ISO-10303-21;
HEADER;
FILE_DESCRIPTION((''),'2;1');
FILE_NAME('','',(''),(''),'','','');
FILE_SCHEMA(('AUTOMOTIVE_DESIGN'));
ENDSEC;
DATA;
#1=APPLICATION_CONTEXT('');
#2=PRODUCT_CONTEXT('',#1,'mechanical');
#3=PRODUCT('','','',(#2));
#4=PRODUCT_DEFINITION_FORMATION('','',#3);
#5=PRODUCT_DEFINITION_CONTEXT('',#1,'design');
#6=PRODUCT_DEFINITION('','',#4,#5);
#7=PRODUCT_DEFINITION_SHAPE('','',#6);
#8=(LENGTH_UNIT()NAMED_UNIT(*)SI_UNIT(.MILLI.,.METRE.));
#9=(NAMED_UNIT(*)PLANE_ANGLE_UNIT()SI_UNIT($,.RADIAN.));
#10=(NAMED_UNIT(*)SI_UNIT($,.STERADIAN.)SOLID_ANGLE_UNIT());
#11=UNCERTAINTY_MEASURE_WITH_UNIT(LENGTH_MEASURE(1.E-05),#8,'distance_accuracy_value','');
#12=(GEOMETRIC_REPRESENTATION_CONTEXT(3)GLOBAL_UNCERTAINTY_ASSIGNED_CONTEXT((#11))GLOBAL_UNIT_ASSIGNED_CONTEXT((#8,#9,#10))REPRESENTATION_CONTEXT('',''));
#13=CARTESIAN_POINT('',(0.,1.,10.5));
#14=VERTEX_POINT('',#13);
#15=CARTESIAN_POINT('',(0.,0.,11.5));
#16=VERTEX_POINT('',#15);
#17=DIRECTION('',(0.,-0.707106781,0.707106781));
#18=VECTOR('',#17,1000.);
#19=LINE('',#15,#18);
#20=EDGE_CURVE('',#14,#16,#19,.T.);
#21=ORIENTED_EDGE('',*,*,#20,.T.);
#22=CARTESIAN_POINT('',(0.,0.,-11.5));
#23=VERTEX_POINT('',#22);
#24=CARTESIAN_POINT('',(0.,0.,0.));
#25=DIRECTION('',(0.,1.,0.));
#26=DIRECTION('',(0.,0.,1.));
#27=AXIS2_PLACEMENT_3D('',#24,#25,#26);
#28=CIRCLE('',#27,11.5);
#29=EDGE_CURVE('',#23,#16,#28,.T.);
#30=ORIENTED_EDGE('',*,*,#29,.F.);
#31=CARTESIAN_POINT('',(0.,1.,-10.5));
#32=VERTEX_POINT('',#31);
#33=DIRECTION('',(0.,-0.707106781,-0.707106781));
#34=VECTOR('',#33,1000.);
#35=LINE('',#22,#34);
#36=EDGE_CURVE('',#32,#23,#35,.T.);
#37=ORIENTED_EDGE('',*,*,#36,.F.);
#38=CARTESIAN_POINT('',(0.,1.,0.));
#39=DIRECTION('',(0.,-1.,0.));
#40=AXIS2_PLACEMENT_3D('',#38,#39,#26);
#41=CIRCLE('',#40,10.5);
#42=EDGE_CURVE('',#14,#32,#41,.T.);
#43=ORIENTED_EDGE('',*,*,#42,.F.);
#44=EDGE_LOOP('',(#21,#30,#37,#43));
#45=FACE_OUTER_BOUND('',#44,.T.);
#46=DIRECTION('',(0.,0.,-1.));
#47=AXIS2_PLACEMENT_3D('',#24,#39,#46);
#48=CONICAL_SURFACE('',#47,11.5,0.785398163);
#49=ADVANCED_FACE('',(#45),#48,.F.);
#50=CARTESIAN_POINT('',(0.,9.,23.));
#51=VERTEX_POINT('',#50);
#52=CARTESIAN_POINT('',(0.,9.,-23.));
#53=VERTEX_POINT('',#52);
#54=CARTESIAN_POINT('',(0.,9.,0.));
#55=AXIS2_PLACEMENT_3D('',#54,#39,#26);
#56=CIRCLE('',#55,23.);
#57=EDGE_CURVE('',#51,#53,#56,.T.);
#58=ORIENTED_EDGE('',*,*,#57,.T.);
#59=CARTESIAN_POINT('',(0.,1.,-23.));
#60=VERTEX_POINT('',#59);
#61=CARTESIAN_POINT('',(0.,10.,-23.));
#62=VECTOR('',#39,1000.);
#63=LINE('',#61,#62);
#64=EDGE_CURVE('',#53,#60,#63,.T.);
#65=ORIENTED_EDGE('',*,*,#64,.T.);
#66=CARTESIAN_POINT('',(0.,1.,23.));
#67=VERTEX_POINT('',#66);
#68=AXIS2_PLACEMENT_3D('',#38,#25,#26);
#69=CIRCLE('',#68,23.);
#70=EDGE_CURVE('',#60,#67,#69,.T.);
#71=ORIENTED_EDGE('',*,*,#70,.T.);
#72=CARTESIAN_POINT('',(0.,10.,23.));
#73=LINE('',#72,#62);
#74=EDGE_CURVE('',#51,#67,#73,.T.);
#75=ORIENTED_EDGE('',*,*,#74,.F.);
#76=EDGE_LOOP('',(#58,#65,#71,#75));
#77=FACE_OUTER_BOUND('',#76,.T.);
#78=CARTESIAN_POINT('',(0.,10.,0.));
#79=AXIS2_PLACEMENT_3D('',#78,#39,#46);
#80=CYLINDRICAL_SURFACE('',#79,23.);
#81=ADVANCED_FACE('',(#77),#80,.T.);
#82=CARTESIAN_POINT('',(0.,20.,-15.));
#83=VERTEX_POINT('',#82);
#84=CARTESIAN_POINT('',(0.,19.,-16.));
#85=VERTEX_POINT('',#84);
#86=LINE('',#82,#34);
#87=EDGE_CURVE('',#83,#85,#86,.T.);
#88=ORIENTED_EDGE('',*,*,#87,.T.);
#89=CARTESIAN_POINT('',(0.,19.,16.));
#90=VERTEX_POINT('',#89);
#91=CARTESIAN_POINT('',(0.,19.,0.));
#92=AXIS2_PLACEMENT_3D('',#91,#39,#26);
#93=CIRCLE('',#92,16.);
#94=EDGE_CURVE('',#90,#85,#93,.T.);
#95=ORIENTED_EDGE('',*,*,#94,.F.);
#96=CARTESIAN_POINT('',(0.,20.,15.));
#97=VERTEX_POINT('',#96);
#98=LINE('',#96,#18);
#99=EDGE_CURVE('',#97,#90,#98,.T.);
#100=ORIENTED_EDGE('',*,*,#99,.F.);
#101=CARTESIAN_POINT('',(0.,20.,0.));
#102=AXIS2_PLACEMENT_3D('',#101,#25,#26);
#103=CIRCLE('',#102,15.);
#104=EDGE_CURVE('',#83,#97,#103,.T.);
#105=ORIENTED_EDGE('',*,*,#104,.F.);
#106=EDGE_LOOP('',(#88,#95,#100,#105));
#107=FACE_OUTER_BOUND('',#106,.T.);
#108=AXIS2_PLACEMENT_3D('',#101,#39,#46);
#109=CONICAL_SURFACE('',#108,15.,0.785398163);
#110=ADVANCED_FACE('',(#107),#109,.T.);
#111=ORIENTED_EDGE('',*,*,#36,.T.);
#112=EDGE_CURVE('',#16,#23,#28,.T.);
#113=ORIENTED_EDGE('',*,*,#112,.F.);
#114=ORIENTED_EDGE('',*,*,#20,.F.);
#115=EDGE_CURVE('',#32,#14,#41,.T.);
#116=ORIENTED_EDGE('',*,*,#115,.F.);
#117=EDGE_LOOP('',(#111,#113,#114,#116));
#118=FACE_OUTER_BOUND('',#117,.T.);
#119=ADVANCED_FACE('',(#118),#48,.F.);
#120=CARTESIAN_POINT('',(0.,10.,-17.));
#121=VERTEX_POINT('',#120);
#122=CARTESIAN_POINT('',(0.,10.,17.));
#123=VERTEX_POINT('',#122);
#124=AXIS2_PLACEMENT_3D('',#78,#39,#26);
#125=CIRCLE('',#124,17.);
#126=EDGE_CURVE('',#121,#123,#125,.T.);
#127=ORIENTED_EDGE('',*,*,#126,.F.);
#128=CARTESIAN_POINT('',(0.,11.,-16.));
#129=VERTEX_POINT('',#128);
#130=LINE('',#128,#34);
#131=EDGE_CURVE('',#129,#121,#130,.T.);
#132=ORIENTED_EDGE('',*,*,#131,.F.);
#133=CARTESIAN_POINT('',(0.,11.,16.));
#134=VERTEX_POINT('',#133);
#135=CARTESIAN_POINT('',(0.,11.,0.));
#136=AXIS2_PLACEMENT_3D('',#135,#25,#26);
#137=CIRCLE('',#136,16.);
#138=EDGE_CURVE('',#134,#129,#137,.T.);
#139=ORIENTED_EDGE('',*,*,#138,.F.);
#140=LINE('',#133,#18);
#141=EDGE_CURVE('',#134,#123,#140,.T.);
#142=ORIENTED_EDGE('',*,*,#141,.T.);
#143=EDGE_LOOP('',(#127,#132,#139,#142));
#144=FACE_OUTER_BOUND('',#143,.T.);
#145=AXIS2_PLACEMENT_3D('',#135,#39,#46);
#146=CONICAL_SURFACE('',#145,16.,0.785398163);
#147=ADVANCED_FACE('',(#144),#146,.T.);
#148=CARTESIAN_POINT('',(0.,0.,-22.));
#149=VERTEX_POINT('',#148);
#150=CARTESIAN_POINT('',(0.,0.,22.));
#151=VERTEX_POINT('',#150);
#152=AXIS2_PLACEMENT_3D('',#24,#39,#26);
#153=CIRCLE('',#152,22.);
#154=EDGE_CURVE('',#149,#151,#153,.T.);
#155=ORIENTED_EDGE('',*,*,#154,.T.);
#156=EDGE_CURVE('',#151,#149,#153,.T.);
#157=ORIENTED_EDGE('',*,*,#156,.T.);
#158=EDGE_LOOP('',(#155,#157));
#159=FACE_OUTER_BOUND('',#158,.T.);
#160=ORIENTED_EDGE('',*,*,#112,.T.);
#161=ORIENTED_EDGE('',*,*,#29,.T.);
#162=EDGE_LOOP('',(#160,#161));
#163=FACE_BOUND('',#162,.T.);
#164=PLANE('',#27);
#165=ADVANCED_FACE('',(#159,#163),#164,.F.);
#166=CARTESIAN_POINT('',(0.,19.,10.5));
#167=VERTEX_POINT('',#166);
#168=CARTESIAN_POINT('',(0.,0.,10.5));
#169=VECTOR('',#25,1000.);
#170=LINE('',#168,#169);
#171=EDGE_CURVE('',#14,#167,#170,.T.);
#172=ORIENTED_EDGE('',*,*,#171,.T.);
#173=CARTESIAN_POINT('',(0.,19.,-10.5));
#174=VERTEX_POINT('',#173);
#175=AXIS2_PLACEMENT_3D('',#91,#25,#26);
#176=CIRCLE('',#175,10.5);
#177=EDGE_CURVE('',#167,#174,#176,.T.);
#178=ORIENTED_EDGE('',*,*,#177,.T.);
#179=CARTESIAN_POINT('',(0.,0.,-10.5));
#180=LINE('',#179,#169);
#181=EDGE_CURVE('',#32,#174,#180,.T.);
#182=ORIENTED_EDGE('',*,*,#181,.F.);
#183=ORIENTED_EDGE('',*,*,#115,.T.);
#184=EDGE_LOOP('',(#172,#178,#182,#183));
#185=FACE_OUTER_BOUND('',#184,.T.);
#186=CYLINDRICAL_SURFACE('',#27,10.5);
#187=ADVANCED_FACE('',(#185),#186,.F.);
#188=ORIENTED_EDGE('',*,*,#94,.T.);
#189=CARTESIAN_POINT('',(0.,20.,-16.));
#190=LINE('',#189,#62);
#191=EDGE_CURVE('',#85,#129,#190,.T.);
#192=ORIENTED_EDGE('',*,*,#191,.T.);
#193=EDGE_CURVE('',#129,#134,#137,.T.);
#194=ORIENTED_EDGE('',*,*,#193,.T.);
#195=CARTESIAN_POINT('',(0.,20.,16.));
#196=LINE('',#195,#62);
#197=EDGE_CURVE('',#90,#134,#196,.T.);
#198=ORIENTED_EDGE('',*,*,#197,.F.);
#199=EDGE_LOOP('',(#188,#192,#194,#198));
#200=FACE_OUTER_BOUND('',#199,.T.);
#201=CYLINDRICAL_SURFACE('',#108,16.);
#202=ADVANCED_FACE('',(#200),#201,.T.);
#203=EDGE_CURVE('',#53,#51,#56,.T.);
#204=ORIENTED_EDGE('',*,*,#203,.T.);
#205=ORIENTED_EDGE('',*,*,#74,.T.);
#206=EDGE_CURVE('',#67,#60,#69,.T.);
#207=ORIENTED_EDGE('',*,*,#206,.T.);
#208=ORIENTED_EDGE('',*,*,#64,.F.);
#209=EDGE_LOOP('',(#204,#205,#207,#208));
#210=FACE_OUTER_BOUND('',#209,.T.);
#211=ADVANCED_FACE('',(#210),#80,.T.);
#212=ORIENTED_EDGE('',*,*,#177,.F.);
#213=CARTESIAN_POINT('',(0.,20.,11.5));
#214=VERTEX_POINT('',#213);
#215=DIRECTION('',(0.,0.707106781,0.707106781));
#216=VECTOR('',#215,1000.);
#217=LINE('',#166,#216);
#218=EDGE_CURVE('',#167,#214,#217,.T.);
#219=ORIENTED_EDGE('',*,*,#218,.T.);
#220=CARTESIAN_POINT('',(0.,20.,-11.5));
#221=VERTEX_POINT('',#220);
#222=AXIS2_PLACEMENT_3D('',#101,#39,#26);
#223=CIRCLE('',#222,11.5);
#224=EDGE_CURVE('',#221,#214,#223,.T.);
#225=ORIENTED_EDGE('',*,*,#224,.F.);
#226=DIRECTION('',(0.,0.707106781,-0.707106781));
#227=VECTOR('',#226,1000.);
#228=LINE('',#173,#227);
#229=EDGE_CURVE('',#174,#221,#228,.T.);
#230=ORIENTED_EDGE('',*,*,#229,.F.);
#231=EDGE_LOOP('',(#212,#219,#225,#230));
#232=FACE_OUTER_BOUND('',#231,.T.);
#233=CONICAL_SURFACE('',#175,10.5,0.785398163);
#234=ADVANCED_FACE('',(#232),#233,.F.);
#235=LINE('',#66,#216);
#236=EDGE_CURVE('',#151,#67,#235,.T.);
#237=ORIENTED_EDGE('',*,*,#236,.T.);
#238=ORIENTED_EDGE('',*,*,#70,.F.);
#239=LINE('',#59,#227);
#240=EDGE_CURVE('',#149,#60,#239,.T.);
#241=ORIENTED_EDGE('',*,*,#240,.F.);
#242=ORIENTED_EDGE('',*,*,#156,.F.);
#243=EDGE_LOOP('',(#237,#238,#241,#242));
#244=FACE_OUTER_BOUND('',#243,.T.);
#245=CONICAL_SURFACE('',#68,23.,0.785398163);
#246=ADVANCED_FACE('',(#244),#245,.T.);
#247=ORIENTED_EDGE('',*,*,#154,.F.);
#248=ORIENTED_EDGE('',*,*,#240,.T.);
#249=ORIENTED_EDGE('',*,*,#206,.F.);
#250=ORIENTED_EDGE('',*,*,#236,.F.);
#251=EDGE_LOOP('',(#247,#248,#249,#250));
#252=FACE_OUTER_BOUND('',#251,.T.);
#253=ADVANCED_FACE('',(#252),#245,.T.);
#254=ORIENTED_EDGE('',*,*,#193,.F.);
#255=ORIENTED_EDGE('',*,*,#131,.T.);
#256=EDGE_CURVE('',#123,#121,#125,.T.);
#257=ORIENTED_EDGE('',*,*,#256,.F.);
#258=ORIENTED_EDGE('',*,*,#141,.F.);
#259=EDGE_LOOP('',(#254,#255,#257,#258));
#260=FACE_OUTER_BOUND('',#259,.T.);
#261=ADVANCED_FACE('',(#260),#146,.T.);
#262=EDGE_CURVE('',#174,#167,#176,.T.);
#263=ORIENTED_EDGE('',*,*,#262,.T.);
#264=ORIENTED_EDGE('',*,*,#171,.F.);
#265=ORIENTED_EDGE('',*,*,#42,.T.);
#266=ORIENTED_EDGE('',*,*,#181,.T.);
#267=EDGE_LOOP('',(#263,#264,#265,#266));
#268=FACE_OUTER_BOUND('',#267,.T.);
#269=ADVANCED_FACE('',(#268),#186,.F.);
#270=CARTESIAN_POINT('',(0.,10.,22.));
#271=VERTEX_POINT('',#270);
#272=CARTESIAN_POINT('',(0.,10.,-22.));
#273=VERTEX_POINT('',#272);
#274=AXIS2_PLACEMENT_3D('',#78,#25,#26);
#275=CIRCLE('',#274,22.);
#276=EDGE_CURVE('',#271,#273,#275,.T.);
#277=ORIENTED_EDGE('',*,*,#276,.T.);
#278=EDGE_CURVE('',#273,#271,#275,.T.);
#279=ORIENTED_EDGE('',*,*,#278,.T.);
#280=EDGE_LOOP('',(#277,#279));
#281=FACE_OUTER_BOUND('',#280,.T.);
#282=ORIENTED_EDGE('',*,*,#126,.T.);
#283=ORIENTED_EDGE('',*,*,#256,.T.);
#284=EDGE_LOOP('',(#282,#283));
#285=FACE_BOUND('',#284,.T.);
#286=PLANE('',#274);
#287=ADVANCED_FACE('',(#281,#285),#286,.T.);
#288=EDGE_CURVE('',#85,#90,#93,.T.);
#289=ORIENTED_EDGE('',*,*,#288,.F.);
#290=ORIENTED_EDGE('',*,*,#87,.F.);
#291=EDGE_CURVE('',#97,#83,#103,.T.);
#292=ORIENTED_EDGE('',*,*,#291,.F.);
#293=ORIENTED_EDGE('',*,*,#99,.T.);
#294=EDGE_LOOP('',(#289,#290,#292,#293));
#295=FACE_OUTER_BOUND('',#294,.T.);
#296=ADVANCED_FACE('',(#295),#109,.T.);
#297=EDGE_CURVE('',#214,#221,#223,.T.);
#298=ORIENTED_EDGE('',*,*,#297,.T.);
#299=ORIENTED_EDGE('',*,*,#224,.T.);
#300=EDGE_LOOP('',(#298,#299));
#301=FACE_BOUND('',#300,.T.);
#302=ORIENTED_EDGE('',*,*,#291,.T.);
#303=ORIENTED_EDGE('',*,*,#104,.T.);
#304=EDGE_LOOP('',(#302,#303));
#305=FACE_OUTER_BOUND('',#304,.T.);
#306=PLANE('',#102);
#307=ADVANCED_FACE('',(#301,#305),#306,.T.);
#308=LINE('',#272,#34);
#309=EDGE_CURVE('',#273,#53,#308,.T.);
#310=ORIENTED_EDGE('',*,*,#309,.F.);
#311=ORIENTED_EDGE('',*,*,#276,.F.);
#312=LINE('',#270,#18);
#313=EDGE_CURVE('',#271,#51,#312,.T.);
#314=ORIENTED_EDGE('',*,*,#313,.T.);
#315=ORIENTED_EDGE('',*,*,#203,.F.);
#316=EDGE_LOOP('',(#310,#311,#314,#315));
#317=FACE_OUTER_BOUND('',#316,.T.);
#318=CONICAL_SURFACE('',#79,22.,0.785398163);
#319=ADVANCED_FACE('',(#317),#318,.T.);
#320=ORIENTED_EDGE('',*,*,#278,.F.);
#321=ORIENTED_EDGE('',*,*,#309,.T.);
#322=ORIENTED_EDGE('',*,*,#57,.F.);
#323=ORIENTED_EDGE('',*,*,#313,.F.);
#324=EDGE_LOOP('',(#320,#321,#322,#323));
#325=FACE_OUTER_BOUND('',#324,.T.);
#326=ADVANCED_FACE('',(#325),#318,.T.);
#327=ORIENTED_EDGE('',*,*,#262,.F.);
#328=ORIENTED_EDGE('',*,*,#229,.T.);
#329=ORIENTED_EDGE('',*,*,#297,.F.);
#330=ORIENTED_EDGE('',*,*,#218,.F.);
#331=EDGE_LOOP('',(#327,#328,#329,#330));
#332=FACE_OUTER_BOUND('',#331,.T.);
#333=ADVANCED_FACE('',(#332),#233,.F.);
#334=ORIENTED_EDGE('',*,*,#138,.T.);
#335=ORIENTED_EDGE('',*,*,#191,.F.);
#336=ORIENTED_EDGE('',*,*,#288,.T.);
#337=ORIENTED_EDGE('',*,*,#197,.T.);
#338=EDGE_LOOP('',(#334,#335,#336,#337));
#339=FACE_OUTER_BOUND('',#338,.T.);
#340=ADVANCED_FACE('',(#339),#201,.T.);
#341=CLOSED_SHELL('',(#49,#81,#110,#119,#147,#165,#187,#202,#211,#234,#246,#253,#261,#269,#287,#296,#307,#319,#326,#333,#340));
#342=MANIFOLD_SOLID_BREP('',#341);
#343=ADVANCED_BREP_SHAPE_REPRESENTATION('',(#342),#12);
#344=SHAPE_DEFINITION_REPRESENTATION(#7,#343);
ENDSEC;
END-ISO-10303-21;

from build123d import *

# Parameters (mm, degrees)
SKETCH1_R           = 23
BOSS_EXTRUDE1_DEPTH = 10
SKETCH2_R           = 16
BOSS_EXTRUDE2_DEPTH = 10
SKETCH3_R           = 10.5
CUT_EXTRUDE1_DEPTH  = 20
CHAMFER1_SIZE       = 1
CHAMFER2_SIZE       = 1


with BuildPart() as part:
    # Sketch1 → Boss-Extrude1 (new body)
    with BuildSketch(Plane(origin=(0, 0, 0), x_dir=(1, 0, 0), z_dir=(0, 1, 0))):
        with Locations(Location((0, 0, 0), (0, 0, 270))):
            Circle(SKETCH1_R)
    extrude(amount=BOSS_EXTRUDE1_DEPTH)

    # Sketch2 → Boss-Extrude2 (add)
    with BuildSketch(Plane(origin=(0, 10, 0), x_dir=(1, 0, 0), z_dir=(0, 1, 0))):
        with Locations(Location((0, 0, 0), (0, 0, 270))):
            Circle(SKETCH2_R)
    extrude(amount=BOSS_EXTRUDE2_DEPTH)

    # Sketch3 → Cut-Extrude1 (cut)
    with BuildSketch(Plane(origin=(0, 20, 0), x_dir=(1, 0, 0), z_dir=(0, 1, 0))):
        with Locations(Location((0, 0, 0), (0, 0, 270))):
            Circle(SKETCH3_R)
    extrude(amount=-CUT_EXTRUDE1_DEPTH, mode=Mode.SUBTRACT)

    # Chamfer1
    chamfer1_edges = [part.edges().sort_by_distance(p)[0] for p in [
        (0, 20, -10.5),
        (0, 0, -23),
        (0, 10, -23),
        (0, 10, -16),
        (0, 20, -16),
    ]]
    chamfer(chamfer1_edges, length=CHAMFER1_SIZE)

    # Chamfer2
    chamfer2_edges = [part.edges().sort_by_distance(p)[0] for p in [
        (0, 0, -10.5),
    ]]
    chamfer(chamfer2_edges, length=CHAMFER2_SIZE)


solid = part.part
